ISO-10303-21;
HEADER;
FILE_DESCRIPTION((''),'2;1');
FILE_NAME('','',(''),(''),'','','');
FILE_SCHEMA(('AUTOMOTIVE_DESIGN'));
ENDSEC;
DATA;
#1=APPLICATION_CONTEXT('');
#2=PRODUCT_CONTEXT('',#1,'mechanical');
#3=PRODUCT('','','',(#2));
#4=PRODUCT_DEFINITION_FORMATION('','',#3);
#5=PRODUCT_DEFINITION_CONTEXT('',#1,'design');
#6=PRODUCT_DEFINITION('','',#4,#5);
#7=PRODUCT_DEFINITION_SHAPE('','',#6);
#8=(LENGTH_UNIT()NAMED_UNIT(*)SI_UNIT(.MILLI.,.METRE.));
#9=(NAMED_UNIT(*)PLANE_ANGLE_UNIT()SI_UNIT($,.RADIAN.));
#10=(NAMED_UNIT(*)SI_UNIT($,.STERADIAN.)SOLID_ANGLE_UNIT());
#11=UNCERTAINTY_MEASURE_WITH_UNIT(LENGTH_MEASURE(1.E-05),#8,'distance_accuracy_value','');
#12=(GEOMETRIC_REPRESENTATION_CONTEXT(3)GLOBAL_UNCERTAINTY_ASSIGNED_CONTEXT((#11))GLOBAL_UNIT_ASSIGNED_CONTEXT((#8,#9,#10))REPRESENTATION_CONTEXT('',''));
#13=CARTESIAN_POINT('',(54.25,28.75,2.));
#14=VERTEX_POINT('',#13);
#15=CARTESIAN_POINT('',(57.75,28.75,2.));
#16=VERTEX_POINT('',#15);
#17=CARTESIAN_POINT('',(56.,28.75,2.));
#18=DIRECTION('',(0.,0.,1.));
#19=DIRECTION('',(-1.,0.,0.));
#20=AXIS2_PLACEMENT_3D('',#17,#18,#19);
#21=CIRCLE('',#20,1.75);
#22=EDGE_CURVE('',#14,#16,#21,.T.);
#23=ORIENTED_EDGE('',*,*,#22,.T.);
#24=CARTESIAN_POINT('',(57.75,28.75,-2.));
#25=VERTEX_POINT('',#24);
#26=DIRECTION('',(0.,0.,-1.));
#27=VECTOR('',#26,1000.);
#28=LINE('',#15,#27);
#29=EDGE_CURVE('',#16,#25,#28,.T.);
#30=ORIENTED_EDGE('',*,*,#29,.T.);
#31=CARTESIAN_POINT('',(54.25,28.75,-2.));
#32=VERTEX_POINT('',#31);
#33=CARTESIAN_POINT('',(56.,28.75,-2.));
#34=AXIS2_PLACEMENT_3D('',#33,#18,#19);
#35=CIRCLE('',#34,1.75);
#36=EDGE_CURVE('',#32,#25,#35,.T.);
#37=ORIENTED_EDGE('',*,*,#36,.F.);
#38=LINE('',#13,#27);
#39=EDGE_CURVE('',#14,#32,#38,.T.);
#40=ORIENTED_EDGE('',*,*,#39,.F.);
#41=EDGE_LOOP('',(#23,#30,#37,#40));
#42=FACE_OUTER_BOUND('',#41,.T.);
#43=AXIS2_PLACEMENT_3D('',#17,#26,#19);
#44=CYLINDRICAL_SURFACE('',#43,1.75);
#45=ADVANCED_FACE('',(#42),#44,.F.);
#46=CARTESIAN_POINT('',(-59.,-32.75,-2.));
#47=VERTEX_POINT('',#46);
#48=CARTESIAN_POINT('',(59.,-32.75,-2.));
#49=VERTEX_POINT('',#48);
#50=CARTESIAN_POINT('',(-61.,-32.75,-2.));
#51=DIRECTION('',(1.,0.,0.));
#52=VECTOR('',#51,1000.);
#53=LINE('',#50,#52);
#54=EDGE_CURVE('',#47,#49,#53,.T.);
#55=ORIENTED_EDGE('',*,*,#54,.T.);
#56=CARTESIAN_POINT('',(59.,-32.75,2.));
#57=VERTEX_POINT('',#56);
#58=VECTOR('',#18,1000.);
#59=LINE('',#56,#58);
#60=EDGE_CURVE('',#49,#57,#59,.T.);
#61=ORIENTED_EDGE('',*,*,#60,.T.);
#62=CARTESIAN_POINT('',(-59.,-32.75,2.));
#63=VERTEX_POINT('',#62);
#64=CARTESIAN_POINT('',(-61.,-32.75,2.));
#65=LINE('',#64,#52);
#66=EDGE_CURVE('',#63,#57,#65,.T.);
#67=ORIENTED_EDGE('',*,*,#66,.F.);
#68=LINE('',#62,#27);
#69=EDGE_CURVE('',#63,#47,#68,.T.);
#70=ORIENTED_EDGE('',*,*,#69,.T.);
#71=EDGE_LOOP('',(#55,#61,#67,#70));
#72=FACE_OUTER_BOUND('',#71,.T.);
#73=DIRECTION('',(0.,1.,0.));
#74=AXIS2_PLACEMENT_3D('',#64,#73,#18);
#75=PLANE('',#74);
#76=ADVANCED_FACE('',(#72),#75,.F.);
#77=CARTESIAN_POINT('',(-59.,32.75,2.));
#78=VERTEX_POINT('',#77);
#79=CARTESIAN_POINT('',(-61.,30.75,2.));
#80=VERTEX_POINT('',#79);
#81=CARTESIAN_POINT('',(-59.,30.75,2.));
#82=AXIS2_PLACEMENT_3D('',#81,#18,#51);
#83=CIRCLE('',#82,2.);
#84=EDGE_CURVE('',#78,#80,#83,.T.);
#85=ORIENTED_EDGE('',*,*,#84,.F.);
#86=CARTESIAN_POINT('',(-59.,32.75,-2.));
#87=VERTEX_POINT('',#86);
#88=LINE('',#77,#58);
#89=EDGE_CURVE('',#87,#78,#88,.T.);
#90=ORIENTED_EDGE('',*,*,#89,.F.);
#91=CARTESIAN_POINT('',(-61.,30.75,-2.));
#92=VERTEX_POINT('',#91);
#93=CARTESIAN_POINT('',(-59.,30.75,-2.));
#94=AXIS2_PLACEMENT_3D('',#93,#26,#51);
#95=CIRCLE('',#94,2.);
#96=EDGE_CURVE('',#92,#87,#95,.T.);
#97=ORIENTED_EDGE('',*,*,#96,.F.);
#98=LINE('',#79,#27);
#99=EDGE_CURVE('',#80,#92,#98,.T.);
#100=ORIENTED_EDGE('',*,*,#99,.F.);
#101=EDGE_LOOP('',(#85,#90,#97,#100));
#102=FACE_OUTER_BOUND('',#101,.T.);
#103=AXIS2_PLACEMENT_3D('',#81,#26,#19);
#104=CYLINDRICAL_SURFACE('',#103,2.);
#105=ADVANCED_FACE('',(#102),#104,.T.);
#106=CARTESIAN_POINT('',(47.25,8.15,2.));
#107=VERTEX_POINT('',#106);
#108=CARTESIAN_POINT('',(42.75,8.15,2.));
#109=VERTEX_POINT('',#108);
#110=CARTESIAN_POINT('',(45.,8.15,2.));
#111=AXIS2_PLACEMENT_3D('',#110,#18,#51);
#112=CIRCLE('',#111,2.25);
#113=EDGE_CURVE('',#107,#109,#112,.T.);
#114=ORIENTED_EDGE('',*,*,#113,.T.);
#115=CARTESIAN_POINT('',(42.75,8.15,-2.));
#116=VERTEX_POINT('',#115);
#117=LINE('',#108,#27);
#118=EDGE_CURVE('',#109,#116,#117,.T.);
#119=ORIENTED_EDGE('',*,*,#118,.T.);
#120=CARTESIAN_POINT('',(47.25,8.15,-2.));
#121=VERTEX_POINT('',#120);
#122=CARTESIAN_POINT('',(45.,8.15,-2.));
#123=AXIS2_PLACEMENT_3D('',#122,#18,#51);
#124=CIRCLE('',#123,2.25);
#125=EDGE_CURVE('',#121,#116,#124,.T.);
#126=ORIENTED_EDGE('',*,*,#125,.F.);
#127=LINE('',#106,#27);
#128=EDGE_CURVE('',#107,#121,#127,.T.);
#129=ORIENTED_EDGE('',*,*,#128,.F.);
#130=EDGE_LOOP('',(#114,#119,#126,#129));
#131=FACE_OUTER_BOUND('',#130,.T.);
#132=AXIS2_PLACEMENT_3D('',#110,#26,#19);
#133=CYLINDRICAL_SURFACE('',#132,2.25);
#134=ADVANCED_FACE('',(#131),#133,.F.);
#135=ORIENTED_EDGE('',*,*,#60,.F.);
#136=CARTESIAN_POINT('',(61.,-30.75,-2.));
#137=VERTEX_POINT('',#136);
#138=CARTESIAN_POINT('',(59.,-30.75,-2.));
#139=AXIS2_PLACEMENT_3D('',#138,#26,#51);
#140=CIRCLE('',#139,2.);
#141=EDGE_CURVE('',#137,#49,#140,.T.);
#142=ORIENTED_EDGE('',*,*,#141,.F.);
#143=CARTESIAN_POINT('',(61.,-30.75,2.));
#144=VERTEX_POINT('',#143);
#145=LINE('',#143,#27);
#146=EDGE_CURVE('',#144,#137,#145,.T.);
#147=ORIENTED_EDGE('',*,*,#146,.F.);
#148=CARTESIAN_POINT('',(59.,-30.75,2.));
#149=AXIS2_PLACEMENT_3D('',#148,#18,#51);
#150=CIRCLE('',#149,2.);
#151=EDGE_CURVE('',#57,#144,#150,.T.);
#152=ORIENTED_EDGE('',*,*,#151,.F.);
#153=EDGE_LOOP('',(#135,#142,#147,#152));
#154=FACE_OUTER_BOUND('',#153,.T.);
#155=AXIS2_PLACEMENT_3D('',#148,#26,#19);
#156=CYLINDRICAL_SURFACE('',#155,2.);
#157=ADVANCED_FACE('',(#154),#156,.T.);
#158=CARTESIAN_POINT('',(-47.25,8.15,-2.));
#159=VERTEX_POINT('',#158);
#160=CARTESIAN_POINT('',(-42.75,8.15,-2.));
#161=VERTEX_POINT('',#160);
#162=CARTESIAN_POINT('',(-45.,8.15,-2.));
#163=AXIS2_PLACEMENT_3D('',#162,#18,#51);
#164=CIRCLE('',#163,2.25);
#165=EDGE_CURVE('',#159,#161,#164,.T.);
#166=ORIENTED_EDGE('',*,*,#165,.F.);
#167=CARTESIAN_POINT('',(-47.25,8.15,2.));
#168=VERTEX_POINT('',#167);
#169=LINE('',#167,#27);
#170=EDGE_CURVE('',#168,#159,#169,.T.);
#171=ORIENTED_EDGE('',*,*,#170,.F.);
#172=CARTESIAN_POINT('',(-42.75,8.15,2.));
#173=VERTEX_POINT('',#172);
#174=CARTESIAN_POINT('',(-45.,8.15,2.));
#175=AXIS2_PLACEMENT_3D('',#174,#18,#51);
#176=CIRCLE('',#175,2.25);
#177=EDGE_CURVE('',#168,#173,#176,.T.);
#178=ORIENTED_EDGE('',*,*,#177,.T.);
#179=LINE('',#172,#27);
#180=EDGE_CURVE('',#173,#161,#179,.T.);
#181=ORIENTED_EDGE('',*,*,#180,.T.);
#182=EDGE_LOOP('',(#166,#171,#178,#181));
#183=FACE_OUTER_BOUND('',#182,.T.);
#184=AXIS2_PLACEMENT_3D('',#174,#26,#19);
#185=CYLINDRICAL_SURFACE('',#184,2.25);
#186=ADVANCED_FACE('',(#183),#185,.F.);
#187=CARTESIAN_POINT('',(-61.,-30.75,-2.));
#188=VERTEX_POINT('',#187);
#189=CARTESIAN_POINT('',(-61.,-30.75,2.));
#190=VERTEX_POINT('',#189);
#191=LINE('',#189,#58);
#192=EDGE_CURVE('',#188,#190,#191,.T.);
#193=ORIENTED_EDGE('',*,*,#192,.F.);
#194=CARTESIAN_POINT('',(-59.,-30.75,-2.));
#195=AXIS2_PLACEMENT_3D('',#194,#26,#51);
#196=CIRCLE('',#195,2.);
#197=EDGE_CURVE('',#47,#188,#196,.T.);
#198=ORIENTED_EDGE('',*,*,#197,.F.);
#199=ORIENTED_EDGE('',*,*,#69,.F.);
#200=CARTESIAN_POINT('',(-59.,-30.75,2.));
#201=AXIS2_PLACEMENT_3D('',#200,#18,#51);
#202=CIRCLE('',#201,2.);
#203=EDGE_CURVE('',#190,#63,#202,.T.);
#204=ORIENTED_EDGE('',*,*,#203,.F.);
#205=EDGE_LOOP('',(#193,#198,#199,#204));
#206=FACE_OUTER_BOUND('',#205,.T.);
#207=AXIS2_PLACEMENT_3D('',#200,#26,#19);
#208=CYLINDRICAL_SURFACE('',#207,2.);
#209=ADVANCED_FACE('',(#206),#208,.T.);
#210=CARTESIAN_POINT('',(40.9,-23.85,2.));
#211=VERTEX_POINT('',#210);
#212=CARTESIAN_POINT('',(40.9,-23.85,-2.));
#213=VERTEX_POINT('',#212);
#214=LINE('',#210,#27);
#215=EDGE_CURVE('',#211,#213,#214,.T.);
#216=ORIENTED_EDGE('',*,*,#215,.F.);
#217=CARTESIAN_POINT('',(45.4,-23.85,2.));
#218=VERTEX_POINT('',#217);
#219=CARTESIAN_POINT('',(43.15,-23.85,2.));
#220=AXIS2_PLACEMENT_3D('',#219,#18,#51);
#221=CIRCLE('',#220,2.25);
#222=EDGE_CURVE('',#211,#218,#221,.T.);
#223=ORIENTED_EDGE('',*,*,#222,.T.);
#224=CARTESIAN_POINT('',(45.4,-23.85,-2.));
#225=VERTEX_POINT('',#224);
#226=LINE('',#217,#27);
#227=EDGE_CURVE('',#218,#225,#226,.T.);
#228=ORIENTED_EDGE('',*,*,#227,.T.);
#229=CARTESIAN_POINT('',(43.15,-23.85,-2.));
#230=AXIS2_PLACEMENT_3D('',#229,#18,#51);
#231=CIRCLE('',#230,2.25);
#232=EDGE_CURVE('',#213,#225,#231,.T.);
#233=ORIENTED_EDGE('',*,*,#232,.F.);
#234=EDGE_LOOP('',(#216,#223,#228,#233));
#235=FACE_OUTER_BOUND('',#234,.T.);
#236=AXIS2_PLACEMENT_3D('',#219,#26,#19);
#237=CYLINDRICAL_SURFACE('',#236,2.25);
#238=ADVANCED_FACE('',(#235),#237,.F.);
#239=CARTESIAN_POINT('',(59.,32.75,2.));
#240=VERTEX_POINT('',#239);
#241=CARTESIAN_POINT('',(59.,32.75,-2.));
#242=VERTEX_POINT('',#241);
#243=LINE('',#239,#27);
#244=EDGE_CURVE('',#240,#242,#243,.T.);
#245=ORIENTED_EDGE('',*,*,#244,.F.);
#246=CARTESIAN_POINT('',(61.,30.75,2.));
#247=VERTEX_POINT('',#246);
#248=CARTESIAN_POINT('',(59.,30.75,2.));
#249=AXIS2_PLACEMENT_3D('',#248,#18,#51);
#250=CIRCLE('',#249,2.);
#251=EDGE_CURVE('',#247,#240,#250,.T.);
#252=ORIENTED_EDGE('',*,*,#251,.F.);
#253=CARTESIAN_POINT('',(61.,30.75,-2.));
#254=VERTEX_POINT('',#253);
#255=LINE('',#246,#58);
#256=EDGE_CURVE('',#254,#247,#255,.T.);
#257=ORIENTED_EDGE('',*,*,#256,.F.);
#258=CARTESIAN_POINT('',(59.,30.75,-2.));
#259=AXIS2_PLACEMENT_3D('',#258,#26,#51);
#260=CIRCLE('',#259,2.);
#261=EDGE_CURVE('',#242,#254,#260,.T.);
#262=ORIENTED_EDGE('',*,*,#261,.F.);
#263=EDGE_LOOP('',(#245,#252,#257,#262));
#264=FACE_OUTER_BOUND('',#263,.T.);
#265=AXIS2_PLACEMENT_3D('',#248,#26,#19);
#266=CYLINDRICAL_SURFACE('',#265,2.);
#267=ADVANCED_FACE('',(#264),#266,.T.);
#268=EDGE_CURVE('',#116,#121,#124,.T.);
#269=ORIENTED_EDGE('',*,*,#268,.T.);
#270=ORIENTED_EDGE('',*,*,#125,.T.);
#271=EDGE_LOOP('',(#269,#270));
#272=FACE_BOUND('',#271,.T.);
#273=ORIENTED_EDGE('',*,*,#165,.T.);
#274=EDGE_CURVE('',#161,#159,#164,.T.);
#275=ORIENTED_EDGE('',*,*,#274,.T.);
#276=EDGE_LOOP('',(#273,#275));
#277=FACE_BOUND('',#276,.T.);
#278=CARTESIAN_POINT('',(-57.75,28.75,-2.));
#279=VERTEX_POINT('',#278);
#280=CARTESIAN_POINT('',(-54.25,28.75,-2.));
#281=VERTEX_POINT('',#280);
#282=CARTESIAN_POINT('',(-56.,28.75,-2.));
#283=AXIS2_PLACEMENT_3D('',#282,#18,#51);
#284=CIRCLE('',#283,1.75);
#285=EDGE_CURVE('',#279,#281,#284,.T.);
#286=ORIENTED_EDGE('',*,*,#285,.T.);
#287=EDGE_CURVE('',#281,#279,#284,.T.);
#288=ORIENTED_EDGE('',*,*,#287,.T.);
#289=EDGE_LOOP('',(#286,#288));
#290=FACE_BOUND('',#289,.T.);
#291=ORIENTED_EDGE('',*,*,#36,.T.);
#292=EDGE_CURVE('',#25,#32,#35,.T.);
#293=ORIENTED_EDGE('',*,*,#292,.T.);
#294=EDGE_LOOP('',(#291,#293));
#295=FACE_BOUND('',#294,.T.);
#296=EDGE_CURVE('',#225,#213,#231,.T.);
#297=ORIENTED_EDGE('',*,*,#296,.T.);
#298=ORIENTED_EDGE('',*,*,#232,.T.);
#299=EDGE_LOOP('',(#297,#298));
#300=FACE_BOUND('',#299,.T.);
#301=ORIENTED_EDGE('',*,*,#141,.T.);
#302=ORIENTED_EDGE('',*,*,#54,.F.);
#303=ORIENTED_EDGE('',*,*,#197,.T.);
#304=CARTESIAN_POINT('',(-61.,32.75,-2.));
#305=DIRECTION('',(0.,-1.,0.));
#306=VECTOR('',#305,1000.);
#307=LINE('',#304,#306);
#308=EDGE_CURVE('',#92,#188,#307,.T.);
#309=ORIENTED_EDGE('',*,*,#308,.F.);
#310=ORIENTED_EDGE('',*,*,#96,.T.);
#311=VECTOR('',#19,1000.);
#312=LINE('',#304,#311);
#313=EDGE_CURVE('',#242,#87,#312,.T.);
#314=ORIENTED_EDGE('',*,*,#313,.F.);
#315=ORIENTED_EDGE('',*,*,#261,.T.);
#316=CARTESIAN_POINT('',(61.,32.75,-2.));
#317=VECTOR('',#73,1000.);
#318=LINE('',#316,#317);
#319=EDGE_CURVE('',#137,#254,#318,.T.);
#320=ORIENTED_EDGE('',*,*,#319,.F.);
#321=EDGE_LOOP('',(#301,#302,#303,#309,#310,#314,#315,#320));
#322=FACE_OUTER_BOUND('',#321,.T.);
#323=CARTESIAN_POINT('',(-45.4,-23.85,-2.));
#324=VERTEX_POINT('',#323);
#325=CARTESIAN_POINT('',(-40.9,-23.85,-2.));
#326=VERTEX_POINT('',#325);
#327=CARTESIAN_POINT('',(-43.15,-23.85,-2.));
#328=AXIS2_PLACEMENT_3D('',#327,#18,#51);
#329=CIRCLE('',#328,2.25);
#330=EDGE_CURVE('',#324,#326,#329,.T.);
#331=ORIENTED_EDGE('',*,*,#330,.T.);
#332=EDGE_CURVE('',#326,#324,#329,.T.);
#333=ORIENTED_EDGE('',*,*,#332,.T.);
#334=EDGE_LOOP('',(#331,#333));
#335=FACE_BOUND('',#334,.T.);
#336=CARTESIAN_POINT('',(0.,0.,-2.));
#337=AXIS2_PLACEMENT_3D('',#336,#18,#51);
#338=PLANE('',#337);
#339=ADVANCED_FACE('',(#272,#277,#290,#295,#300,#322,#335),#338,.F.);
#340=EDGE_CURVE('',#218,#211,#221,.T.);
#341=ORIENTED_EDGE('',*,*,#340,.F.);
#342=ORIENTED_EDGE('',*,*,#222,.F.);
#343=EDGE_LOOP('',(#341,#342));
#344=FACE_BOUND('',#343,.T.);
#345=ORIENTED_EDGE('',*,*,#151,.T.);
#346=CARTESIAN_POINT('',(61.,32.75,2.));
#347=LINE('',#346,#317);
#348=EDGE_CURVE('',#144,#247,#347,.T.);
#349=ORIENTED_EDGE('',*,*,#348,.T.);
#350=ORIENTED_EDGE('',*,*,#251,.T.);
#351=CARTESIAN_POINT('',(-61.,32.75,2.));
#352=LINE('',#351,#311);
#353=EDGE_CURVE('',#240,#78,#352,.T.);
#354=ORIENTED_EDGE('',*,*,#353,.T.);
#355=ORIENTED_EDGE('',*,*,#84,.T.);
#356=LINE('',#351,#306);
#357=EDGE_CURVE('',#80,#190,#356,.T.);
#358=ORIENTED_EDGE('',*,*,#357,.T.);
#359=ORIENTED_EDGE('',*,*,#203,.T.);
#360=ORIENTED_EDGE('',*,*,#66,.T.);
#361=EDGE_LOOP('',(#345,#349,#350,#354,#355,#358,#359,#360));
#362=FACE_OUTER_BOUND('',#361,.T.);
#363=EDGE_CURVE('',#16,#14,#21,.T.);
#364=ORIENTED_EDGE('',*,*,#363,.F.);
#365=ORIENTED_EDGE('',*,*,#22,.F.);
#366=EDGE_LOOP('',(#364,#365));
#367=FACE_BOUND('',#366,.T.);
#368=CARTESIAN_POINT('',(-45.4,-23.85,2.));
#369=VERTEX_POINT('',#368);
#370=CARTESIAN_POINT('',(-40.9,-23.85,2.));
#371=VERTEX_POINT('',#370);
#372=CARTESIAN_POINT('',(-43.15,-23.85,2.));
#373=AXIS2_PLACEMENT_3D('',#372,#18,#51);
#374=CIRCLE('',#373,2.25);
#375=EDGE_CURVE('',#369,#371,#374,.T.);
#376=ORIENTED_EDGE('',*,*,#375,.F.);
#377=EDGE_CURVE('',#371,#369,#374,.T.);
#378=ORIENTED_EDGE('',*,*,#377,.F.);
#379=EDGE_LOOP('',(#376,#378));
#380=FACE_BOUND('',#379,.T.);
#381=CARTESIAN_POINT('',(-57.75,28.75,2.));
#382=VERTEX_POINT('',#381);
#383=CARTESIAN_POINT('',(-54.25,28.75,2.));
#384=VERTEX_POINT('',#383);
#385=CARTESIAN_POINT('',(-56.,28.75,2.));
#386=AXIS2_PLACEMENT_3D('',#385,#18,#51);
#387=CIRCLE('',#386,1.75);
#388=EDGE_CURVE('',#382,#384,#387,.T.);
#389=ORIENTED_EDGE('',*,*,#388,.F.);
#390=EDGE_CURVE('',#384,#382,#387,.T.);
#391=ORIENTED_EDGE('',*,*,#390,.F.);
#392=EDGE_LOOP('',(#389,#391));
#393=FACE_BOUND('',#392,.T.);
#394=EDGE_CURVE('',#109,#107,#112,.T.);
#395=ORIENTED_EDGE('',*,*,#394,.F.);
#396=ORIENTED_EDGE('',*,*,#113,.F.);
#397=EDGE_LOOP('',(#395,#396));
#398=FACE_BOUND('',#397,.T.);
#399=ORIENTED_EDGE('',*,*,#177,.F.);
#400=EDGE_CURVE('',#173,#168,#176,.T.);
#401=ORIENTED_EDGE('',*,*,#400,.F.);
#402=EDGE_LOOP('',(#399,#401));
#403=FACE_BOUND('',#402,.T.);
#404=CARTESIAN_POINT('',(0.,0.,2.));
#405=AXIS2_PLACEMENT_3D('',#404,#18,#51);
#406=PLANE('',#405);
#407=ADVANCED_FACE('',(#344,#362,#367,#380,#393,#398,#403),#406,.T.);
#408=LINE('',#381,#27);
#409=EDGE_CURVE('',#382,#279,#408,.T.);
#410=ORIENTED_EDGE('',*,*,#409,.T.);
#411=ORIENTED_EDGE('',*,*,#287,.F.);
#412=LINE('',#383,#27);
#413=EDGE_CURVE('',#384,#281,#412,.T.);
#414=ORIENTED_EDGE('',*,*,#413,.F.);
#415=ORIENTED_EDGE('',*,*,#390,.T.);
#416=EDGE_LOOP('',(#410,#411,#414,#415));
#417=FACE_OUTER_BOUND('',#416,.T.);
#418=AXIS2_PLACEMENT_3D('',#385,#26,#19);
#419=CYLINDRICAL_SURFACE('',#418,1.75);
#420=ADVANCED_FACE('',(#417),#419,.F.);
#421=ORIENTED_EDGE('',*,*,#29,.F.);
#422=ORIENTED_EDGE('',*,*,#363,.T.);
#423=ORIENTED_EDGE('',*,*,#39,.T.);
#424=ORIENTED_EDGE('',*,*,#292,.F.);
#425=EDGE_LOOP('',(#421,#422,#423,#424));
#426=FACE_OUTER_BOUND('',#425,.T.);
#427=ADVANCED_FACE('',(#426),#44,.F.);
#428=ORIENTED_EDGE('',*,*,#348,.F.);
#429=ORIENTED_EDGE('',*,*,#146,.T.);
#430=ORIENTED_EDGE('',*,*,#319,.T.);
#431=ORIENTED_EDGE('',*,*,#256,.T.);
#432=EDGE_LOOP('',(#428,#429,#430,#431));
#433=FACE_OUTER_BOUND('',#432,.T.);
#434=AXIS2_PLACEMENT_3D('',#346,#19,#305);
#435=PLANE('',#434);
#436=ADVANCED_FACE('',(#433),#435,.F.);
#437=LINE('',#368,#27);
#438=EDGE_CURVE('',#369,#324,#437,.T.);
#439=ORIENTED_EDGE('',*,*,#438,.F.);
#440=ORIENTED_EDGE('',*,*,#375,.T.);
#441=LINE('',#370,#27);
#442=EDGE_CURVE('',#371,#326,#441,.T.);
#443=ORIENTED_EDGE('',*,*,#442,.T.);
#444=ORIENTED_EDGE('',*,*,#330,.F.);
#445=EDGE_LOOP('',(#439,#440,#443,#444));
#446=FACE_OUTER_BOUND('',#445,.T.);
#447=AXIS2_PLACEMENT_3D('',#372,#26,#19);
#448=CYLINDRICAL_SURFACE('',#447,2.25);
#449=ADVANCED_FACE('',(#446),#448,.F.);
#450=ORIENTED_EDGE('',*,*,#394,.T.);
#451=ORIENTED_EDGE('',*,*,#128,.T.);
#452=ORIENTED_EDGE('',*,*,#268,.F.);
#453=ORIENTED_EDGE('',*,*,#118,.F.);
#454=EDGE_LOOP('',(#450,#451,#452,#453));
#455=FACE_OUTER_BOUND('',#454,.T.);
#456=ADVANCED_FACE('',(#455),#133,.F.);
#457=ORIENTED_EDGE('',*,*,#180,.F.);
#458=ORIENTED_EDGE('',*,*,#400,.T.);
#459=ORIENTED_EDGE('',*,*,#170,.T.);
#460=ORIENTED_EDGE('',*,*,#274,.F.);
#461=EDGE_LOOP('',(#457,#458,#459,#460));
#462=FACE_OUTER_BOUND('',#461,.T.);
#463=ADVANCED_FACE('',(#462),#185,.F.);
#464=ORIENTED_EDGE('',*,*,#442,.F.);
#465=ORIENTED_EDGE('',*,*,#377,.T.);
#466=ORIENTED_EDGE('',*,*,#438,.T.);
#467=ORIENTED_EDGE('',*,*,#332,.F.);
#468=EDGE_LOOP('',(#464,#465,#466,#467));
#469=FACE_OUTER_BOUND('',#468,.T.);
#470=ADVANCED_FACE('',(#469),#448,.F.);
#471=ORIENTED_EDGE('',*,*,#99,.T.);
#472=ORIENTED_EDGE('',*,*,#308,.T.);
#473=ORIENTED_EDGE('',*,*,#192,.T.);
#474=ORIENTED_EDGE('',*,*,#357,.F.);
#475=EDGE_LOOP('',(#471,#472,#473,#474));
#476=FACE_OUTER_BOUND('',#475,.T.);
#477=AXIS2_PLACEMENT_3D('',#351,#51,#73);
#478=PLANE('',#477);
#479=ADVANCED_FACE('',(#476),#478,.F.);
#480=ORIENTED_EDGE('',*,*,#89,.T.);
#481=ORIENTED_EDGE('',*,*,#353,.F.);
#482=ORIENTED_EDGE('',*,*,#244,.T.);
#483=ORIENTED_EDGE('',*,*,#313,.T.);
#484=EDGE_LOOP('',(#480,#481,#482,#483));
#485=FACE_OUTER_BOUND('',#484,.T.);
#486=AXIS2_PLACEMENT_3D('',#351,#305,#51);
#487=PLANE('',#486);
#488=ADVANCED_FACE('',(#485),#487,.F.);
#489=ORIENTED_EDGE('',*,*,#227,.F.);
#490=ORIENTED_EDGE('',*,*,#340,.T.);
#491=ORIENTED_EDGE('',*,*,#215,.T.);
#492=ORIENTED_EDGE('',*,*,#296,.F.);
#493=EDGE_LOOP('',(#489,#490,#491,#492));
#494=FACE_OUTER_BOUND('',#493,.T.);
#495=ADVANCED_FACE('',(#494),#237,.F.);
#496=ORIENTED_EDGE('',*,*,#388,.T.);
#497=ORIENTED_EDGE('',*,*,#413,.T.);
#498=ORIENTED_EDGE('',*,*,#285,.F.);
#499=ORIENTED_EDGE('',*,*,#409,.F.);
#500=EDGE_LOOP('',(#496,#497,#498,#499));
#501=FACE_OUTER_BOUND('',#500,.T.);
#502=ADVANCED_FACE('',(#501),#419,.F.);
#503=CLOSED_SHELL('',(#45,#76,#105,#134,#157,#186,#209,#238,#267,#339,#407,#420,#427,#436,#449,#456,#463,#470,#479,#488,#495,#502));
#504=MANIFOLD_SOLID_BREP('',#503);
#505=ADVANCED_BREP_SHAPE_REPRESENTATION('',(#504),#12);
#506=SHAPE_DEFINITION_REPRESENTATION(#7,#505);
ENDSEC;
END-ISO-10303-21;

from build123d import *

# Parameters (mm, degrees)
SKETCH_1_W      = 122
SKETCH_1_H      = 65.5
SKETCH_1_R      = 1.75
SKETCH_1_R_2    = 2.25
EXTRUDE_1_DEPTH = 2
FILLET_1_R      = 2


with BuildPart() as part:
    # 草图1 → 凸台-拉伸1 (new, symmetric)
    with BuildSketch(Plane.XY):
        Rectangle(SKETCH_1_W, SKETCH_1_H)
        with Locations((-56, 28.75)):
            Circle(SKETCH_1_R, mode=Mode.SUBTRACT)
        with Locations((-45, 8.15)):
            Circle(SKETCH_1_R_2, mode=Mode.SUBTRACT)
        with Locations((45, 8.15)):
            Circle(SKETCH_1_R_2, mode=Mode.SUBTRACT)
        with Locations(Location((56, 28.75, 0), (0, 0, 180))):
            Circle(SKETCH_1_R, mode=Mode.SUBTRACT)
        with Locations((-43.15, -23.85)):
            Circle(SKETCH_1_R_2, mode=Mode.SUBTRACT)
        with Locations((43.15, -23.85)):
            Circle(SKETCH_1_R_2, mode=Mode.SUBTRACT)
    extrude(amount=EXTRUDE_1_DEPTH, both=True)

    # 圆角1
    fillet_1_edges = [part.edges().sort_by_distance(p)[0] for p in [
        (61, -32.75, 0),
        (-61, -32.75, 0),
        (-61, 32.75, 0),
        (61, 32.75, 0),
    ]]
    fillet(fillet_1_edges, radius=FILLET_1_R)


solid = part.part
